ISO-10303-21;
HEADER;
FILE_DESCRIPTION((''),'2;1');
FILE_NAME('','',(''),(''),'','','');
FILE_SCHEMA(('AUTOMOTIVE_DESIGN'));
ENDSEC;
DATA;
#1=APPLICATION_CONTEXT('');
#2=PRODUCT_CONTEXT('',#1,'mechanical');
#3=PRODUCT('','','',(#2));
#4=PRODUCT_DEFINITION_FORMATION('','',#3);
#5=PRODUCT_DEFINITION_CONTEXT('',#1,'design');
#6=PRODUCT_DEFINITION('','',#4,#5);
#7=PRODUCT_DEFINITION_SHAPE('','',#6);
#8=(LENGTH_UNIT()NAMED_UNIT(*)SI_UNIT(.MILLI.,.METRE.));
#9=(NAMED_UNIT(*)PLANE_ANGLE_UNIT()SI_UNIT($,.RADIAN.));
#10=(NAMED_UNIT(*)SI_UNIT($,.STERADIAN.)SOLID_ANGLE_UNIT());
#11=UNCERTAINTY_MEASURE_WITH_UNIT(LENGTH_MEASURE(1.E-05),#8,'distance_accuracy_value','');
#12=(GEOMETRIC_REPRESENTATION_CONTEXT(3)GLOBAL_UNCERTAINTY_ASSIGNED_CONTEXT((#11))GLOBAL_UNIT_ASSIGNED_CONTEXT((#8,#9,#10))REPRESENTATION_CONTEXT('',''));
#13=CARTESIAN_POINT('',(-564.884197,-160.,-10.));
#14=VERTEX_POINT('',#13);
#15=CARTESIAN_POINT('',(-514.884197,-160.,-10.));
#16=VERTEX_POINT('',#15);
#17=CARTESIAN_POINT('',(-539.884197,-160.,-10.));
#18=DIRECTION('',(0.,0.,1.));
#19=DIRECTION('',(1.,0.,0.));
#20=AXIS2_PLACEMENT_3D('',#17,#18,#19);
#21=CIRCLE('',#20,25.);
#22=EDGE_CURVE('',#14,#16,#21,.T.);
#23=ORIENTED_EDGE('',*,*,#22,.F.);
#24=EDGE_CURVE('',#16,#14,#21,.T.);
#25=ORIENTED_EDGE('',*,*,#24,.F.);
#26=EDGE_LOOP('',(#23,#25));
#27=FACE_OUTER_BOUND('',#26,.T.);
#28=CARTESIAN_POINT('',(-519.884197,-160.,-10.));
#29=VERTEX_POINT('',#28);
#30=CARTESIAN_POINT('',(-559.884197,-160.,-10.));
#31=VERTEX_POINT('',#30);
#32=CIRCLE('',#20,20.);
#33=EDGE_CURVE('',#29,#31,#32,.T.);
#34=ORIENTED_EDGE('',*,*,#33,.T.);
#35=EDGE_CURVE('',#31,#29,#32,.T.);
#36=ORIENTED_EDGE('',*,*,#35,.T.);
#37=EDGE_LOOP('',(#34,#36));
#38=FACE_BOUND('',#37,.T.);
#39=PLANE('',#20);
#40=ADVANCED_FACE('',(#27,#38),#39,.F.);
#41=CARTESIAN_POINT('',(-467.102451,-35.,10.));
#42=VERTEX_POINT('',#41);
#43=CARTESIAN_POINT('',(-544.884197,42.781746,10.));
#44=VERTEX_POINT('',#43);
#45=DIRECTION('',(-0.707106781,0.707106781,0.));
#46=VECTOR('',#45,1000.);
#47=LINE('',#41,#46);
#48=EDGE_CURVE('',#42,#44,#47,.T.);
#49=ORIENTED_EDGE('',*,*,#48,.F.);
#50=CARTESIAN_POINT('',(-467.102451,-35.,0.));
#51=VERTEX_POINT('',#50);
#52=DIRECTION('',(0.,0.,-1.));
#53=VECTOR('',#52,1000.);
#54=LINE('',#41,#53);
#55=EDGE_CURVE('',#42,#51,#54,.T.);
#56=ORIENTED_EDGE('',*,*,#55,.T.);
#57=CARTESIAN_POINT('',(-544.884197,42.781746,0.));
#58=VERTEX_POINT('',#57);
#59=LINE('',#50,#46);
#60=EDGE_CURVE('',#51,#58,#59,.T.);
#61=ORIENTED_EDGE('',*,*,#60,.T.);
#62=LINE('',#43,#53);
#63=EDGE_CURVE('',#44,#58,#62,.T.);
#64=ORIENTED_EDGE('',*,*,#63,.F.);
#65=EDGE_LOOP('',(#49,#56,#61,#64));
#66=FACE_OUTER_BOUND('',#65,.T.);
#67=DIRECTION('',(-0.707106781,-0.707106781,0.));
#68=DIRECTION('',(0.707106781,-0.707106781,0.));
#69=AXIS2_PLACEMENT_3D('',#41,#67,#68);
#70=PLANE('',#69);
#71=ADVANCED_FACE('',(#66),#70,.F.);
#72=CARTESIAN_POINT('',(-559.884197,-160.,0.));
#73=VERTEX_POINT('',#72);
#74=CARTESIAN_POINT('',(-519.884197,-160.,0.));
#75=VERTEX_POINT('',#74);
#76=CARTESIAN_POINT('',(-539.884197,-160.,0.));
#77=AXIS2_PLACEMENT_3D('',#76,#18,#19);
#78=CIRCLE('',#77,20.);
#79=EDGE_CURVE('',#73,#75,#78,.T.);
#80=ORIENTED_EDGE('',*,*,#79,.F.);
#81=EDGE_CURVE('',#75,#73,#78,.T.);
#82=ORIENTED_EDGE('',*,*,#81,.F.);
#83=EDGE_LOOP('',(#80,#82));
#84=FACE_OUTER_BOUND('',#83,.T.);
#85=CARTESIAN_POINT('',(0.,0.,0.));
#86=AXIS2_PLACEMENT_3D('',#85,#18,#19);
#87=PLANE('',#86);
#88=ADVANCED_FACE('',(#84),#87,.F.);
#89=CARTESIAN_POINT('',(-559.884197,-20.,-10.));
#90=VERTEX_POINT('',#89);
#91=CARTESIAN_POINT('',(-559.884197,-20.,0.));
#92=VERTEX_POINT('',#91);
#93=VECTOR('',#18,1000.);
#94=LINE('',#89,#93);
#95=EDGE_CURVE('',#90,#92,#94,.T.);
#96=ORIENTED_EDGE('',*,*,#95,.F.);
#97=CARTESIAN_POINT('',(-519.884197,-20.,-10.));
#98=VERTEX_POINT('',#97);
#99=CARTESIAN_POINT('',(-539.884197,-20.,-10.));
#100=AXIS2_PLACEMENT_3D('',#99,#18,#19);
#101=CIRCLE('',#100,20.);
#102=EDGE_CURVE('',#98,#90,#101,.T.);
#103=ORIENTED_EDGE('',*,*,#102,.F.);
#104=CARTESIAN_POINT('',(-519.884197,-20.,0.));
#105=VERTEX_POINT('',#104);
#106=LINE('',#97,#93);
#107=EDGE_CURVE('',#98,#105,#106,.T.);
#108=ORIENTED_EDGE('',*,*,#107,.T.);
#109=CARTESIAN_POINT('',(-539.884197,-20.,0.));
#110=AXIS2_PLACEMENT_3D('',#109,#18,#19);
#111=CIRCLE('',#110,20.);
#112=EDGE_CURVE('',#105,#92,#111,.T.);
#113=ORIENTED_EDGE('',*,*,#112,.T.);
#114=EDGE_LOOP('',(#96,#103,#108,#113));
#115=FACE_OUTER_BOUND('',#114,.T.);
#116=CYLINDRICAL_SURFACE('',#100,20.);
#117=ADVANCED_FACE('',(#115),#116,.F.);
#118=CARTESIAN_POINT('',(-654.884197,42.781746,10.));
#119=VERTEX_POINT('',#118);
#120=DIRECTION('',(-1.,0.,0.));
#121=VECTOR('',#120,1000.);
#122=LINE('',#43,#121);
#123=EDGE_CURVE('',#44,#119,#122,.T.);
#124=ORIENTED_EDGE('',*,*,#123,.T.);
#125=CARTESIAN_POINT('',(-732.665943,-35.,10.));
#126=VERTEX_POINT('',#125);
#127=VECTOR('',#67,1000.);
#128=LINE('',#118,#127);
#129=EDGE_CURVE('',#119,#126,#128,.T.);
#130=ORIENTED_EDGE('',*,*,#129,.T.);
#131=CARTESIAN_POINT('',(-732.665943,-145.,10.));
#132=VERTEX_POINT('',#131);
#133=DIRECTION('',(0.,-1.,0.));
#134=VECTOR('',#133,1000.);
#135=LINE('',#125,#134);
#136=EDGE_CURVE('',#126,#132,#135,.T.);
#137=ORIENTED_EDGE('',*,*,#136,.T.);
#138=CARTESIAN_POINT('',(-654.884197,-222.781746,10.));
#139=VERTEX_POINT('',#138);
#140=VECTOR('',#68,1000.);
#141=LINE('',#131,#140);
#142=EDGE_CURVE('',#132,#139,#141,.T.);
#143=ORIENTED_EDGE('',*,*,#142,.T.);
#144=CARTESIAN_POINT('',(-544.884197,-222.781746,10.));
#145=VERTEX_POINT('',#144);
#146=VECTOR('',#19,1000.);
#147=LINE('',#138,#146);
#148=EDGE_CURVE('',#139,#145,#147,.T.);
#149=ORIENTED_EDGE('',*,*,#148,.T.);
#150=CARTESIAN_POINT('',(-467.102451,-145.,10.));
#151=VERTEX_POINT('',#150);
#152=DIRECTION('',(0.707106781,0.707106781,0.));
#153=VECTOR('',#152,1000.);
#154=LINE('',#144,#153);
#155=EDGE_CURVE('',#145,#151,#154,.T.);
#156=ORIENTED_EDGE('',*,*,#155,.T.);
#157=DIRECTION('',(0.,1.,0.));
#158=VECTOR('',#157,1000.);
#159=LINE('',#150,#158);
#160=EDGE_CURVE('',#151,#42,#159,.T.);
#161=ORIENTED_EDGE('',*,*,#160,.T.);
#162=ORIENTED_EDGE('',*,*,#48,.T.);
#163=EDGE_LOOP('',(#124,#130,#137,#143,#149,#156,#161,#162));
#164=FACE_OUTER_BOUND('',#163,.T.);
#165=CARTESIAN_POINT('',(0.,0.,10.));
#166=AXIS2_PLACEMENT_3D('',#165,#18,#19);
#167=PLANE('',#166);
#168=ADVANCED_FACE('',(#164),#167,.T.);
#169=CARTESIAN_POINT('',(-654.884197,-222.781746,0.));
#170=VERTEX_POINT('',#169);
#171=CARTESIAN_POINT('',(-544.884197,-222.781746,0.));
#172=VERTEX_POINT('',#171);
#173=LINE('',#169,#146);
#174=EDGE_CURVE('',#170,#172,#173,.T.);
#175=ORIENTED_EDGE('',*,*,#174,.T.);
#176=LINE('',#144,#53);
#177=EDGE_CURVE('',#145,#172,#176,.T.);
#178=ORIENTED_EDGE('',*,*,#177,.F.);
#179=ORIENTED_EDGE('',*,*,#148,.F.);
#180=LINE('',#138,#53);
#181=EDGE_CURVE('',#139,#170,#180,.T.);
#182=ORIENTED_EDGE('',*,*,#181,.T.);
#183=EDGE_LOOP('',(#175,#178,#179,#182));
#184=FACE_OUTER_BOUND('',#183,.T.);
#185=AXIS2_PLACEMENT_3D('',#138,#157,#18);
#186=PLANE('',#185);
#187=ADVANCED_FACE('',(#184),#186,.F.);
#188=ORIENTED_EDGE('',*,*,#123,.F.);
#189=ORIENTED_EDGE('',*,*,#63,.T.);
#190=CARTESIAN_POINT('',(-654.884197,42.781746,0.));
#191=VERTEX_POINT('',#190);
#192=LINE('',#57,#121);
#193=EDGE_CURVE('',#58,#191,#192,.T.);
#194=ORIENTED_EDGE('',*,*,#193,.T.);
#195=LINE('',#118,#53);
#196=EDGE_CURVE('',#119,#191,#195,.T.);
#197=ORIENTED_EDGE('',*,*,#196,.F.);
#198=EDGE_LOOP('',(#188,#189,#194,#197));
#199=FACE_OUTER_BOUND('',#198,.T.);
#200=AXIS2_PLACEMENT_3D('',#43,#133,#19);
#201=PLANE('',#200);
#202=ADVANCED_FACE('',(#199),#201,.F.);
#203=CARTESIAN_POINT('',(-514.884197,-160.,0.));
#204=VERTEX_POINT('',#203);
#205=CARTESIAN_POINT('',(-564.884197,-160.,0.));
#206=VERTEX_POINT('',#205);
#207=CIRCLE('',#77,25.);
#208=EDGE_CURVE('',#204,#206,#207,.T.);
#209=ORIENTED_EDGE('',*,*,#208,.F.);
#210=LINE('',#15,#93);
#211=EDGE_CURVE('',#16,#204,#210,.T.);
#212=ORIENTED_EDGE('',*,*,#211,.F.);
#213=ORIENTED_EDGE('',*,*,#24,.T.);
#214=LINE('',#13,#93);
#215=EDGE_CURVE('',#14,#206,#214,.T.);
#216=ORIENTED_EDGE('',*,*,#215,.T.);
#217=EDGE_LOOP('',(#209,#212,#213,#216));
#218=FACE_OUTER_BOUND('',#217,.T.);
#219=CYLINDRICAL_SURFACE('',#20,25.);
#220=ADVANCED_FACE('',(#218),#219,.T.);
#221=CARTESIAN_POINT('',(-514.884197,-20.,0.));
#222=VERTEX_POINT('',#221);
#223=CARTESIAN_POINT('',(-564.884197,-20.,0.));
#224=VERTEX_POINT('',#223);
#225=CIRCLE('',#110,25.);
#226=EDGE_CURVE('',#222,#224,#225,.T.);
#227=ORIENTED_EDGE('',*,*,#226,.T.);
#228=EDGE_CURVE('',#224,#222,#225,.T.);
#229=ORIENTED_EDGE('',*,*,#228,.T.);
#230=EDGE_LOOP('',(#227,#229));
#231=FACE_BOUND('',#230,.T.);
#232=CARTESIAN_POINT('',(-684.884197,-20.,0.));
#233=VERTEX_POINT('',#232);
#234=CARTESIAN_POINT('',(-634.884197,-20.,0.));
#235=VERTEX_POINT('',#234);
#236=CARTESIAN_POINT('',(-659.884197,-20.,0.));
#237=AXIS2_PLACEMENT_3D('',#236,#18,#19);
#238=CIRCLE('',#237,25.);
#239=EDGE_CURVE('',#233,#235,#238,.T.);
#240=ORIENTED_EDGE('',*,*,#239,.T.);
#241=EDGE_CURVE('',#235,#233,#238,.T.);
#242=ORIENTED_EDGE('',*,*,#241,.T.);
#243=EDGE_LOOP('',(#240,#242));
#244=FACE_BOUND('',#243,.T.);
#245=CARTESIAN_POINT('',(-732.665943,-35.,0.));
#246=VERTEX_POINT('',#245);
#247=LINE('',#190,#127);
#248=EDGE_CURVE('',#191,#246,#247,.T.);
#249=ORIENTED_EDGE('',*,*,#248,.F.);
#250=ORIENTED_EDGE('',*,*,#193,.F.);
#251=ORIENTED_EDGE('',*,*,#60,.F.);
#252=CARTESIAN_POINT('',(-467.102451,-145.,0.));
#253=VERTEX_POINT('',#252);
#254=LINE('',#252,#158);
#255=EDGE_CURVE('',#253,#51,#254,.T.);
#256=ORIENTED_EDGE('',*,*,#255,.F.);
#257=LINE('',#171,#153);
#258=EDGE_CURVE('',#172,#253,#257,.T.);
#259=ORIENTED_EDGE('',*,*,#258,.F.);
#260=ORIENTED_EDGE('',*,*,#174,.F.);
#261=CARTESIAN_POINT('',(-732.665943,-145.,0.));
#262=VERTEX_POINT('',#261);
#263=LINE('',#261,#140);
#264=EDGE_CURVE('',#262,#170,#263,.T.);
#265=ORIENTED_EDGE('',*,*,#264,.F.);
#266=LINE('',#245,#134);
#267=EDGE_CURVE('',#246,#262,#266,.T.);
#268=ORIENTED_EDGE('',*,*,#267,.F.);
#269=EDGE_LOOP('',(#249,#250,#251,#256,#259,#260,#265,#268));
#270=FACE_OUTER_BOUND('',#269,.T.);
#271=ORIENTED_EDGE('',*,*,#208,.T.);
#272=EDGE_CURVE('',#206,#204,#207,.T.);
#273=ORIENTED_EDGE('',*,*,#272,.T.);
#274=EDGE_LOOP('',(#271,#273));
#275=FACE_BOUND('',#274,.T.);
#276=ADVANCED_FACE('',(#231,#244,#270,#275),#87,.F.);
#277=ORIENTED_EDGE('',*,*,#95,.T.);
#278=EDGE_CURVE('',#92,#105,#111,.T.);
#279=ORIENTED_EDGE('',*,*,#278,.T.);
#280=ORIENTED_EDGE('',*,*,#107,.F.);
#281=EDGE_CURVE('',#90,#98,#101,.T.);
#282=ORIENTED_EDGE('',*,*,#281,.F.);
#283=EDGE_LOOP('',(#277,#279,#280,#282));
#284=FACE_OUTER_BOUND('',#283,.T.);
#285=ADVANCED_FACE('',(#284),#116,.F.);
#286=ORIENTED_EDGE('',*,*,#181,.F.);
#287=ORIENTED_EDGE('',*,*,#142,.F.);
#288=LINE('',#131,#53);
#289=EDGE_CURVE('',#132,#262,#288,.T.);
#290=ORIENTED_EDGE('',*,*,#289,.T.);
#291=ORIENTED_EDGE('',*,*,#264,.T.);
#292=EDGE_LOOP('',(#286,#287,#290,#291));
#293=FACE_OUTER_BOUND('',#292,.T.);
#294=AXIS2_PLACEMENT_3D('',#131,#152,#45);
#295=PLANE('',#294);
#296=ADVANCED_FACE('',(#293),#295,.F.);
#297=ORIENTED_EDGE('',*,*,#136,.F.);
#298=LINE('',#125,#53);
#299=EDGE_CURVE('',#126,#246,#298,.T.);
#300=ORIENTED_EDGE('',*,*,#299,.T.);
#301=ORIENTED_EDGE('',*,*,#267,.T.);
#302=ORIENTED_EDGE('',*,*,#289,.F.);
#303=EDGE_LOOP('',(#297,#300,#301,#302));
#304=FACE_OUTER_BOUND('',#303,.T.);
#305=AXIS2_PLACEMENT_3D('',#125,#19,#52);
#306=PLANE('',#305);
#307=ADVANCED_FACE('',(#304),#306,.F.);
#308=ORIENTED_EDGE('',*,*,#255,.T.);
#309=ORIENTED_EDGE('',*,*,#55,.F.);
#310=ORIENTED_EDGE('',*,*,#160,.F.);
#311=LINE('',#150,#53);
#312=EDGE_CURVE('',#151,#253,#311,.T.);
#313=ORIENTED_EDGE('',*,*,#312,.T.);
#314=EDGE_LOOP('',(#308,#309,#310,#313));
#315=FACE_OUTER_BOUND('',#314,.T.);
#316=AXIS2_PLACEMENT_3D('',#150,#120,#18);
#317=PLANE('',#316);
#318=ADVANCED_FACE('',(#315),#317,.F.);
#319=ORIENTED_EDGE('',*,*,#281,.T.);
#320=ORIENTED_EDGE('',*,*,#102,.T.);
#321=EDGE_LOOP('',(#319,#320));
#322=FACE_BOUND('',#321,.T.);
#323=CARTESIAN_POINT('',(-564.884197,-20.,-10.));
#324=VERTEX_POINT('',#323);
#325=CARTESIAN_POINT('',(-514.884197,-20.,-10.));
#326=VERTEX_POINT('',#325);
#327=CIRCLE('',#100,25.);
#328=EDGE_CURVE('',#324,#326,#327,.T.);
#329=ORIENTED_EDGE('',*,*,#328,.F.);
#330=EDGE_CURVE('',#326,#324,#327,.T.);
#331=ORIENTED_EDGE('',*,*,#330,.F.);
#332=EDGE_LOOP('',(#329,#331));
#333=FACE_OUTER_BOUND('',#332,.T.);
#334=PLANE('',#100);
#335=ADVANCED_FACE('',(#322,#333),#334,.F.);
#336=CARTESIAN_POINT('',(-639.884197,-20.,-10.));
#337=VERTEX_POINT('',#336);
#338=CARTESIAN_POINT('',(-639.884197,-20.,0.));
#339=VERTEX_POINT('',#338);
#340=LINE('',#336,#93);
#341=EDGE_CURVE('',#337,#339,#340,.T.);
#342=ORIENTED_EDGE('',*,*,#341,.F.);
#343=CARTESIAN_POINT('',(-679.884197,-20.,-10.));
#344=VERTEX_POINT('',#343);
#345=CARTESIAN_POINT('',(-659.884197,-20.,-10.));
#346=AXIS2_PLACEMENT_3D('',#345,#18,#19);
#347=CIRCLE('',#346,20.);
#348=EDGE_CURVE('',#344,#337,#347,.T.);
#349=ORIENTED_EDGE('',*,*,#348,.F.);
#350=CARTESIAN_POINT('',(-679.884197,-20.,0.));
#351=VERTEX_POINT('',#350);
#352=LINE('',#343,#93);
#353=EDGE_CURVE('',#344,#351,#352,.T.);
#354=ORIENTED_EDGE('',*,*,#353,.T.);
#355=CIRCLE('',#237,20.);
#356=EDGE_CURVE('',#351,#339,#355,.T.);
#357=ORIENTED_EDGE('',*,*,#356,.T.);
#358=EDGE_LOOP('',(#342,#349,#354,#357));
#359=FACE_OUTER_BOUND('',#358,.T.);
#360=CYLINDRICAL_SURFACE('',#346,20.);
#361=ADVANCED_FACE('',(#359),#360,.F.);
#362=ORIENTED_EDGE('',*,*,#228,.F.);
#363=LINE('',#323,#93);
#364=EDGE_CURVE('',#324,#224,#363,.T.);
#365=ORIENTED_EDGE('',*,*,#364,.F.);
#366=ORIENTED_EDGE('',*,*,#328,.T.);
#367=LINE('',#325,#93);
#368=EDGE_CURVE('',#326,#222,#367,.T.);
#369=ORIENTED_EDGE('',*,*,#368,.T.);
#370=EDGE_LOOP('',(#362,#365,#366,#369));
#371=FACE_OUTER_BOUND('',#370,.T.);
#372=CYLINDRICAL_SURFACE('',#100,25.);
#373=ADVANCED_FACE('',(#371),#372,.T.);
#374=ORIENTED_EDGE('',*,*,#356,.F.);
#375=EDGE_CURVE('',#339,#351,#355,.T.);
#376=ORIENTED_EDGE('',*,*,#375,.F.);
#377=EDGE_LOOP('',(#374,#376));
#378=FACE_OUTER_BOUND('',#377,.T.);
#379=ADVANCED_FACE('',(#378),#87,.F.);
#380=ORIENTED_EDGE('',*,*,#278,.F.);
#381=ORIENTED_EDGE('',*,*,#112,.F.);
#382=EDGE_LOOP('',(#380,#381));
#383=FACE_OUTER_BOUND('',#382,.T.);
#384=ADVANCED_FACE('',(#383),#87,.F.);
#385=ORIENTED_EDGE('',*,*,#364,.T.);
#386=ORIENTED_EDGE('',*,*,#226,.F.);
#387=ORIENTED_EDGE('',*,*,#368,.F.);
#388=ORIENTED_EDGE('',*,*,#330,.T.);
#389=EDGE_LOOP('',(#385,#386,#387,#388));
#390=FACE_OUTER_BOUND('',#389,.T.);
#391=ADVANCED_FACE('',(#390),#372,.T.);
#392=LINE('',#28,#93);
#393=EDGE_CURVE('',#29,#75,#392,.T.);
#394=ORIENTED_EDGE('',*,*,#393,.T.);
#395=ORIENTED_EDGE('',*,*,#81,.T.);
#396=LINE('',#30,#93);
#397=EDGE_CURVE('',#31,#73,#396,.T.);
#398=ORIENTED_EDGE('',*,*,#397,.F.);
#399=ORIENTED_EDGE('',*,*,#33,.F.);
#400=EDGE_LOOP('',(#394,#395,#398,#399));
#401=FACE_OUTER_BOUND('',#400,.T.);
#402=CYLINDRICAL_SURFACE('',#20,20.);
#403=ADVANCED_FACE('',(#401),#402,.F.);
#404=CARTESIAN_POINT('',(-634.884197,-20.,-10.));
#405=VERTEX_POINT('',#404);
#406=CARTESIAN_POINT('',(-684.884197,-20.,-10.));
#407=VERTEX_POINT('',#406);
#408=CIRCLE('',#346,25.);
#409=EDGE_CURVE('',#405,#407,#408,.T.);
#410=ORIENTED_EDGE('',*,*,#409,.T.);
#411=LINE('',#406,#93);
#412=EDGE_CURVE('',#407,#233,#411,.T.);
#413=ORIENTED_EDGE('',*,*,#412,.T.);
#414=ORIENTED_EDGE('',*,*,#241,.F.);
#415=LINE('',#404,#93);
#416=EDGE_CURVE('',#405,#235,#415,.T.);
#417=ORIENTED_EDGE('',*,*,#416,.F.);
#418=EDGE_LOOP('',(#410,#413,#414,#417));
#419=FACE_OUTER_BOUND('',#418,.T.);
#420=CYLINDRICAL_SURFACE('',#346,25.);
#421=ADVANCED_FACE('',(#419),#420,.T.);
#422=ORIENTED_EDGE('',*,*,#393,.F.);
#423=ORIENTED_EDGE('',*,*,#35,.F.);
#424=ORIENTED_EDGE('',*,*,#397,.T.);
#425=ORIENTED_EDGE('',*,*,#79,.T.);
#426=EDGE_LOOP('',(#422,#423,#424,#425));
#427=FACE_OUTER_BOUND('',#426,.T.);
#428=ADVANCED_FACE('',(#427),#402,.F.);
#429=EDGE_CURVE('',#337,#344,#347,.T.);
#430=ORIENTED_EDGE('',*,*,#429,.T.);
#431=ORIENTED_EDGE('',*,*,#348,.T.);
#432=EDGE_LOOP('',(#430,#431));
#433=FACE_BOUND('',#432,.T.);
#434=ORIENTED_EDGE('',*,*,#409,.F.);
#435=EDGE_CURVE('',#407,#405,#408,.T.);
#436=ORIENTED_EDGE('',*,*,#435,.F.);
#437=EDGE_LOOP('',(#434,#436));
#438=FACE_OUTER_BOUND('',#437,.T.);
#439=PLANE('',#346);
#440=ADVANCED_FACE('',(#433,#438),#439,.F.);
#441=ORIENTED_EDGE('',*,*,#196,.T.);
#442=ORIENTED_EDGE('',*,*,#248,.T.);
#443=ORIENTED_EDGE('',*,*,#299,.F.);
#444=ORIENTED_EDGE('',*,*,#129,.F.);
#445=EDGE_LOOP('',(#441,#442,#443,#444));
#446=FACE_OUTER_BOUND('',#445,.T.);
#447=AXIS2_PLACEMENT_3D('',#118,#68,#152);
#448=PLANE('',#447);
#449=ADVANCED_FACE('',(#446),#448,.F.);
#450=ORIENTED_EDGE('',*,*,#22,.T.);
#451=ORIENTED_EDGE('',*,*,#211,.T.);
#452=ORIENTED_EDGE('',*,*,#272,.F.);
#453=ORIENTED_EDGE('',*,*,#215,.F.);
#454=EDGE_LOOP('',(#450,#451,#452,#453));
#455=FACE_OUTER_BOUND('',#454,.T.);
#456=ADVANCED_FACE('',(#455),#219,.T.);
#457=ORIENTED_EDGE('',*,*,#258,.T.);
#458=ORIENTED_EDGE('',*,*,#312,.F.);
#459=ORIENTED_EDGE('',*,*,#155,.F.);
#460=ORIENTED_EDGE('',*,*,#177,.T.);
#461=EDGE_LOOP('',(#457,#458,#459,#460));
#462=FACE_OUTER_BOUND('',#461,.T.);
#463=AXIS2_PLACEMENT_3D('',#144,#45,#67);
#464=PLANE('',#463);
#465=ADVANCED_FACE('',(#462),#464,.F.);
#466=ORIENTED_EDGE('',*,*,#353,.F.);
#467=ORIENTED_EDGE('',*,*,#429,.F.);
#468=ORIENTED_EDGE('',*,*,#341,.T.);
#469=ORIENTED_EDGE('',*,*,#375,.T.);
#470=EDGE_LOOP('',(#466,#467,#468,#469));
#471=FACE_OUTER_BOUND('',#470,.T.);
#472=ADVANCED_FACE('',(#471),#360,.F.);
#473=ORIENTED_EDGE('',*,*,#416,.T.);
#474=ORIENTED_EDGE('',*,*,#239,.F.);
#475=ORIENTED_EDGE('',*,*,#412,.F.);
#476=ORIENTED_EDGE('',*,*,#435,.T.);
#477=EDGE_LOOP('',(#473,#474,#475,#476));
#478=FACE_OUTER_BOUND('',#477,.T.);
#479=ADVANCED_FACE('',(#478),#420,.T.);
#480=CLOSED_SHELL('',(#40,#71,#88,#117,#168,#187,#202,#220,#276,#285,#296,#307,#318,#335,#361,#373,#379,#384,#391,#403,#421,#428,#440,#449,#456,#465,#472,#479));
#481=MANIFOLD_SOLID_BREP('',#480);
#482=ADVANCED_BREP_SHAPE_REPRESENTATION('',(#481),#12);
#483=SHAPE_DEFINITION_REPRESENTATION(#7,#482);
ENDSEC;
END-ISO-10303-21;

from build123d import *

# Parameters (mm, degrees)
SKETCH1_R             = 25
SKETCH1_R_2           = 20
BOSS_EXTRUDE1_DEPTH   = 10
BOSS_EXTRUDE1_2_DEPTH = 10
BOSS_EXTRUDE1_3_DEPTH = 10
BOSS_EXTRUDE2_DEPTH   = 10


with BuildPart() as part:
    # Sketch1 → Boss-Extrude1 (new body)
    with BuildSketch(Plane.XY):
        with Locations((-659.884196758, -20)):
            Circle(SKETCH1_R)
        with Locations((-659.884196758, -20)):
            Circle(SKETCH1_R_2, mode=Mode.SUBTRACT)
    extrude(amount=-BOSS_EXTRUDE1_DEPTH)



with BuildPart() as body_2:
    # Sketch1 → Boss-Extrude1 2 (new body)
    with BuildSketch(Plane.XY):
        with Locations((-539.884196758, -20)):
            Circle(SKETCH1_R)
        with Locations((-539.884196758, -20)):
            Circle(SKETCH1_R_2, mode=Mode.SUBTRACT)
    extrude(amount=-BOSS_EXTRUDE1_2_DEPTH)


with BuildPart() as body_3:
    # Sketch1 → Boss-Extrude1 3 (new body)
    with BuildSketch(Plane.XY):
        with Locations((-539.884196758, -160)):
            Circle(SKETCH1_R)
        with Locations((-539.884196758, -160)):
            Circle(SKETCH1_R_2, mode=Mode.SUBTRACT)
    extrude(amount=-BOSS_EXTRUDE1_3_DEPTH)


with BuildPart() as part_1:
    add(part.part)

    add(body_2.part)  # Boss-Extrude2 merges body 2

    add(body_3.part)  # Boss-Extrude2 merges body 3
    # Sketch2 → Boss-Extrude2 (add)
    with BuildSketch(Plane.XY):
        Polygon((-544.884196758, -222.781745931), (-467.102450828, -145), (-467.102450828, -35), (-544.884196758, 42.781745931), (-654.884196758, 42.781745931), (-732.665942689, -35), (-732.665942689, -145), (-654.884196758, -222.781745931), align=None)
    extrude(amount=BOSS_EXTRUDE2_DEPTH)


solid = part_1.part
